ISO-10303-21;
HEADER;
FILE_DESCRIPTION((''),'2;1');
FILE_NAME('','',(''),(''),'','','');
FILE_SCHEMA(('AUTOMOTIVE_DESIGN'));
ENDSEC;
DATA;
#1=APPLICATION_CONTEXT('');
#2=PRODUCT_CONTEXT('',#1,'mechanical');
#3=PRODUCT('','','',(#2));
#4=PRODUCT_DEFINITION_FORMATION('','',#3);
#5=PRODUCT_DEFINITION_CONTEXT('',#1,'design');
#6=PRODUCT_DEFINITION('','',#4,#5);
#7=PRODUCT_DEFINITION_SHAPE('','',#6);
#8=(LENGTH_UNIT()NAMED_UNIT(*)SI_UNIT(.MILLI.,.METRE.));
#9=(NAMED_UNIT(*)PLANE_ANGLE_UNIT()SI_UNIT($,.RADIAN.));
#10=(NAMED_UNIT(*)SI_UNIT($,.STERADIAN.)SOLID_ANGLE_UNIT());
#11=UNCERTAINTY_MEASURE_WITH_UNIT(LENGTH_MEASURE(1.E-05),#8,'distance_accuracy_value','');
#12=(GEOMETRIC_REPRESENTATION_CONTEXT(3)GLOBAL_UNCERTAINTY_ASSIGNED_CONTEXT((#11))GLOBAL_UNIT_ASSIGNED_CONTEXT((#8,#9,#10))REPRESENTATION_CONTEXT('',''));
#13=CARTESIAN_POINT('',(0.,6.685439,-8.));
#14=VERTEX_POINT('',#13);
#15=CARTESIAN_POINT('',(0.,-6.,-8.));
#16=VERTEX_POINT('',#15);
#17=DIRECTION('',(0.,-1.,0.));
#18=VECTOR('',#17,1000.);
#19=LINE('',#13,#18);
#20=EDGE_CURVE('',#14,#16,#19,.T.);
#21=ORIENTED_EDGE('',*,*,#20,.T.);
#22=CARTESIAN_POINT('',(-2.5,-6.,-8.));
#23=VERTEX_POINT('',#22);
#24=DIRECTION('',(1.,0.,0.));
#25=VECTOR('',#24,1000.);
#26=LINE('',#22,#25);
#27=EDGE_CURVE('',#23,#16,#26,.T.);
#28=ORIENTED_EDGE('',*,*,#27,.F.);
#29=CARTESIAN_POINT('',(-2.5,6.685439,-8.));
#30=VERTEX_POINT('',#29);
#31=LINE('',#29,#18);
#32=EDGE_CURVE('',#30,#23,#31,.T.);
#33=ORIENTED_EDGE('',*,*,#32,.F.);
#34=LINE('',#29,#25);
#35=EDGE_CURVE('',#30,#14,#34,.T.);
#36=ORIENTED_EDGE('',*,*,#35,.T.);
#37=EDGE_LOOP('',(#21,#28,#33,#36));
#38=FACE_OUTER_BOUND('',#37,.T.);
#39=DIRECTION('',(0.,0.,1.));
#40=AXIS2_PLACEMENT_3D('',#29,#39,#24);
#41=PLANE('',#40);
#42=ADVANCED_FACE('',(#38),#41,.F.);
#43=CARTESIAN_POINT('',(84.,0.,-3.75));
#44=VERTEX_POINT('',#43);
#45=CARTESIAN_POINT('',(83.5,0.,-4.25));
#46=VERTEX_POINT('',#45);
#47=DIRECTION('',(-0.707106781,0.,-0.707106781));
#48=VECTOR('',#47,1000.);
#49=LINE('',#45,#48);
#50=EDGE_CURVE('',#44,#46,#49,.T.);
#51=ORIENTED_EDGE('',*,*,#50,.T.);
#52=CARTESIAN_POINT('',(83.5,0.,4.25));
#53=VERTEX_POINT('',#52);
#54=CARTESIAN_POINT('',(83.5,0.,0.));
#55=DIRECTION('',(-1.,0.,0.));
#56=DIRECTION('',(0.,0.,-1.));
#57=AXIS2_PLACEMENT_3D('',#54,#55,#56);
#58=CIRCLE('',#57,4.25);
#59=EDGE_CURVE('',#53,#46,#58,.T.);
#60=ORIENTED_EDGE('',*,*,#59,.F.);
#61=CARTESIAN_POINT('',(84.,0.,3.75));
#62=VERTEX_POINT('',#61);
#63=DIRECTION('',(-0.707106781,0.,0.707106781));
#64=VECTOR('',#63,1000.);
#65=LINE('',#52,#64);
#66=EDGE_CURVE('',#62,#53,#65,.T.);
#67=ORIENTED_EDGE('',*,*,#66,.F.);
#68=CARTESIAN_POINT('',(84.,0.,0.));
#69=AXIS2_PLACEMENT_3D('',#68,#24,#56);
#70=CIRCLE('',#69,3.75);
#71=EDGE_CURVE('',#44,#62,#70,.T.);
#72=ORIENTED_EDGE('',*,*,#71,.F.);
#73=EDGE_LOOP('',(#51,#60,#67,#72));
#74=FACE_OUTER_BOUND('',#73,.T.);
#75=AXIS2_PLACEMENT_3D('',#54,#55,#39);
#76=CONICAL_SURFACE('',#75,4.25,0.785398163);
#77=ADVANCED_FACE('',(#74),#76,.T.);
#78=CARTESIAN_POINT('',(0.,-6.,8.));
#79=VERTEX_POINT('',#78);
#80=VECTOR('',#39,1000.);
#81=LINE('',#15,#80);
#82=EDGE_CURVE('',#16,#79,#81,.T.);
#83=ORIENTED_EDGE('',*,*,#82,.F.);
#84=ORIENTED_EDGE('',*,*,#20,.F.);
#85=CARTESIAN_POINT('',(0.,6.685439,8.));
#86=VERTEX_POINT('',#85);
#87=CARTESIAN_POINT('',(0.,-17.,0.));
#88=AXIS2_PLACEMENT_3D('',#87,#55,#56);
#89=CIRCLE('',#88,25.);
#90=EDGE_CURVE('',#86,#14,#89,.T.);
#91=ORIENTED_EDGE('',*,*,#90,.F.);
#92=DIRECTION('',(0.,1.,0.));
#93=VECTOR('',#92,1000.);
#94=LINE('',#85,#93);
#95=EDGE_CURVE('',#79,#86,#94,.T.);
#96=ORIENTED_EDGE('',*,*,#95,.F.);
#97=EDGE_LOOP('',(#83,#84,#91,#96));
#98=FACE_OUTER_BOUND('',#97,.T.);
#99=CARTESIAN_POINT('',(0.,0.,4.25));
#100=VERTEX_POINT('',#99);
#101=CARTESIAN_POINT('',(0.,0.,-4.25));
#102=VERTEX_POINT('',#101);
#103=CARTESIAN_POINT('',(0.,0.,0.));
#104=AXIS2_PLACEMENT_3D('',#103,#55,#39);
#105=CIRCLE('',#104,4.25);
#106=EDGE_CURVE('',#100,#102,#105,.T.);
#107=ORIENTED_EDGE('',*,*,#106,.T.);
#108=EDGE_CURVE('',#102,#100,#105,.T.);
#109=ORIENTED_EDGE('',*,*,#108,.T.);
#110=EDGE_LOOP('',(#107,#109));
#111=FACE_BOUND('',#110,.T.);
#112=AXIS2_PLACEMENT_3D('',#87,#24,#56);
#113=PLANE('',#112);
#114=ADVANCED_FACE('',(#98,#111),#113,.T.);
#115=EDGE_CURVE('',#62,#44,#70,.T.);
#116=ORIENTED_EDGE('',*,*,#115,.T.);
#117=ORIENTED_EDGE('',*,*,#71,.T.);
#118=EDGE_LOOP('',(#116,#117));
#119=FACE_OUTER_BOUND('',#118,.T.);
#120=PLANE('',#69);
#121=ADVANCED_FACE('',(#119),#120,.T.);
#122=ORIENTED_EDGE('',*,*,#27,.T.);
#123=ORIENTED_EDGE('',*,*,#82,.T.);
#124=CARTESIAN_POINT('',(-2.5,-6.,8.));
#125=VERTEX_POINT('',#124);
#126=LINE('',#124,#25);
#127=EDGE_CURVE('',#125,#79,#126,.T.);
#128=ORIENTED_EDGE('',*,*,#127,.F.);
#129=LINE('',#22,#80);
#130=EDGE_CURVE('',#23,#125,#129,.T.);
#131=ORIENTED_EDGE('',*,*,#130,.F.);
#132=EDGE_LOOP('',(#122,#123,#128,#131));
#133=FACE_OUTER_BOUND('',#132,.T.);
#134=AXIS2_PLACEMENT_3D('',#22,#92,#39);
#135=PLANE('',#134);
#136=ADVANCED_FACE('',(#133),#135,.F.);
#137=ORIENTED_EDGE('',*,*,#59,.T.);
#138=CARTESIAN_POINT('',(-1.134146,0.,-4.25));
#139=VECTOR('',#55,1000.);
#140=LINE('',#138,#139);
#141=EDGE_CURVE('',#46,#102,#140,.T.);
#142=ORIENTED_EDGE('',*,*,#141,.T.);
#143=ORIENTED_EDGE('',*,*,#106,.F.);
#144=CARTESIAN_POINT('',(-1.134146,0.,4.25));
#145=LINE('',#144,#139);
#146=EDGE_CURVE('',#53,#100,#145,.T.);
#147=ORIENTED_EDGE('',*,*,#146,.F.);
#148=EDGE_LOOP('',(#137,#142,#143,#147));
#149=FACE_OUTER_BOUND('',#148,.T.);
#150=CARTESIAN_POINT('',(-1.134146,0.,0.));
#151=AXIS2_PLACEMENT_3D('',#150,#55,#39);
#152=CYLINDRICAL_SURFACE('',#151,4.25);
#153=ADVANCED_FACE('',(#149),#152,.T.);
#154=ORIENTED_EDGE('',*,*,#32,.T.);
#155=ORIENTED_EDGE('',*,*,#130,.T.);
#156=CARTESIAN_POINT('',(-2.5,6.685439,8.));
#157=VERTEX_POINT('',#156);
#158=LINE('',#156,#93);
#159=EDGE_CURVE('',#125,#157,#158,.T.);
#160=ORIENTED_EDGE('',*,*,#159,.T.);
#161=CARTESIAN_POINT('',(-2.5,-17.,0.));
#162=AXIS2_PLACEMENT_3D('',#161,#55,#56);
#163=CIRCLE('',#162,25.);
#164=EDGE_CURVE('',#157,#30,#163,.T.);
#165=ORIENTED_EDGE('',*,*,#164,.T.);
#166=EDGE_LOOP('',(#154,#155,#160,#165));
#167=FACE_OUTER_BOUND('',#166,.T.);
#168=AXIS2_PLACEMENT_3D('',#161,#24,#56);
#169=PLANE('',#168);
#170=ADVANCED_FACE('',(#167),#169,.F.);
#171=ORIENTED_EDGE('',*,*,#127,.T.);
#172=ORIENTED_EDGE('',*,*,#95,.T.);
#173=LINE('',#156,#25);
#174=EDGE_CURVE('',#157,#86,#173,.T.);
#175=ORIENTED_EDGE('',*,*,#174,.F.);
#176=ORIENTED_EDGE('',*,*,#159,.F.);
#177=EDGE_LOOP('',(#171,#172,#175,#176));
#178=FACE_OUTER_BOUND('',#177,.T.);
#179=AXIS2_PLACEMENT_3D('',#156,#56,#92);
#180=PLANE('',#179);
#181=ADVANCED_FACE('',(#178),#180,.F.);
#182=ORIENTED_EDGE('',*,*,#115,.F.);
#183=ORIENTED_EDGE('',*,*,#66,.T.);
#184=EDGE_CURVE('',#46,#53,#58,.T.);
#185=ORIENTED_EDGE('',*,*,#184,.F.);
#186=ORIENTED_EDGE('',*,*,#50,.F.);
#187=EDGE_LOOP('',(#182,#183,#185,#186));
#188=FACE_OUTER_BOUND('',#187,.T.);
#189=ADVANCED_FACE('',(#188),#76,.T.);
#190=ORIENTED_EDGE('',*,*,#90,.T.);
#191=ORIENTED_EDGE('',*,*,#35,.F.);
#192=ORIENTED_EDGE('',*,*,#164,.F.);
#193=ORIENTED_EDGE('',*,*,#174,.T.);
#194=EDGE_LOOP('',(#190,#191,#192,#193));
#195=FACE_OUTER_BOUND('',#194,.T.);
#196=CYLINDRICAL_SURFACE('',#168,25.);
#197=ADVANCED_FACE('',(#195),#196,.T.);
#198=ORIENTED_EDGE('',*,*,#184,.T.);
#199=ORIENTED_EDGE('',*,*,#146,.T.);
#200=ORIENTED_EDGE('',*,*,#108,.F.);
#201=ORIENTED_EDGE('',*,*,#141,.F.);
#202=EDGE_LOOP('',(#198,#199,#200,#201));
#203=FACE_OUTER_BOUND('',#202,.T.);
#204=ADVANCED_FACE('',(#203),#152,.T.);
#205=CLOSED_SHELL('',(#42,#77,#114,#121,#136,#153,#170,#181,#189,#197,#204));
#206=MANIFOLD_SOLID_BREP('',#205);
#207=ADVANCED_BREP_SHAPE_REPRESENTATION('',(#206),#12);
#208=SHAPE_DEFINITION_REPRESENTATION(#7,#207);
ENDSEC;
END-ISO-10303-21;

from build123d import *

# Parameters (mm, degrees)
SKETCH_1_W      = 84
SKETCH_1_H      = 4.25
CHAMFER_1_SIZE  = 0.5
EXTRUDE_1_DEPTH = 2.5


with BuildPart() as part:
    # 草图1 → 旋转1 (revolve)
    with BuildSketch(Plane.XY, mode=Mode.PRIVATE) as revolve_1_sk:
        with Locations((42, -2.125)):
            Rectangle(SKETCH_1_W, SKETCH_1_H)
    revolve(revolve_1_sk.sketch.rotate(Axis((-1.134146341, 0, 0), (1, 0, 0)), 270), axis=Axis((-1.134146341, 0, 0), (1, 0, 0)))

    # 倒角1
    chamfer_1_edges = [part.edges().sort_by_distance(p)[0] for p in [
        (84, 0, -4.25),
    ]]
    chamfer(chamfer_1_edges, length=CHAMFER_1_SIZE)

    # 草图2 → 凸台-拉伸1 (add)
    with BuildSketch(Plane.ZY):
        with BuildLine():
            Line((-8, 6.685438565), (-8, -6))
            Line((-8, -6), (8, -6))
            Line((8, -6), (8, 6.685438565))
            ThreePointArc((8, 6.685438565), (0, 8), (-8, 6.685438565))
        make_face()
    extrude(amount=EXTRUDE_1_DEPTH)


solid = part.part
